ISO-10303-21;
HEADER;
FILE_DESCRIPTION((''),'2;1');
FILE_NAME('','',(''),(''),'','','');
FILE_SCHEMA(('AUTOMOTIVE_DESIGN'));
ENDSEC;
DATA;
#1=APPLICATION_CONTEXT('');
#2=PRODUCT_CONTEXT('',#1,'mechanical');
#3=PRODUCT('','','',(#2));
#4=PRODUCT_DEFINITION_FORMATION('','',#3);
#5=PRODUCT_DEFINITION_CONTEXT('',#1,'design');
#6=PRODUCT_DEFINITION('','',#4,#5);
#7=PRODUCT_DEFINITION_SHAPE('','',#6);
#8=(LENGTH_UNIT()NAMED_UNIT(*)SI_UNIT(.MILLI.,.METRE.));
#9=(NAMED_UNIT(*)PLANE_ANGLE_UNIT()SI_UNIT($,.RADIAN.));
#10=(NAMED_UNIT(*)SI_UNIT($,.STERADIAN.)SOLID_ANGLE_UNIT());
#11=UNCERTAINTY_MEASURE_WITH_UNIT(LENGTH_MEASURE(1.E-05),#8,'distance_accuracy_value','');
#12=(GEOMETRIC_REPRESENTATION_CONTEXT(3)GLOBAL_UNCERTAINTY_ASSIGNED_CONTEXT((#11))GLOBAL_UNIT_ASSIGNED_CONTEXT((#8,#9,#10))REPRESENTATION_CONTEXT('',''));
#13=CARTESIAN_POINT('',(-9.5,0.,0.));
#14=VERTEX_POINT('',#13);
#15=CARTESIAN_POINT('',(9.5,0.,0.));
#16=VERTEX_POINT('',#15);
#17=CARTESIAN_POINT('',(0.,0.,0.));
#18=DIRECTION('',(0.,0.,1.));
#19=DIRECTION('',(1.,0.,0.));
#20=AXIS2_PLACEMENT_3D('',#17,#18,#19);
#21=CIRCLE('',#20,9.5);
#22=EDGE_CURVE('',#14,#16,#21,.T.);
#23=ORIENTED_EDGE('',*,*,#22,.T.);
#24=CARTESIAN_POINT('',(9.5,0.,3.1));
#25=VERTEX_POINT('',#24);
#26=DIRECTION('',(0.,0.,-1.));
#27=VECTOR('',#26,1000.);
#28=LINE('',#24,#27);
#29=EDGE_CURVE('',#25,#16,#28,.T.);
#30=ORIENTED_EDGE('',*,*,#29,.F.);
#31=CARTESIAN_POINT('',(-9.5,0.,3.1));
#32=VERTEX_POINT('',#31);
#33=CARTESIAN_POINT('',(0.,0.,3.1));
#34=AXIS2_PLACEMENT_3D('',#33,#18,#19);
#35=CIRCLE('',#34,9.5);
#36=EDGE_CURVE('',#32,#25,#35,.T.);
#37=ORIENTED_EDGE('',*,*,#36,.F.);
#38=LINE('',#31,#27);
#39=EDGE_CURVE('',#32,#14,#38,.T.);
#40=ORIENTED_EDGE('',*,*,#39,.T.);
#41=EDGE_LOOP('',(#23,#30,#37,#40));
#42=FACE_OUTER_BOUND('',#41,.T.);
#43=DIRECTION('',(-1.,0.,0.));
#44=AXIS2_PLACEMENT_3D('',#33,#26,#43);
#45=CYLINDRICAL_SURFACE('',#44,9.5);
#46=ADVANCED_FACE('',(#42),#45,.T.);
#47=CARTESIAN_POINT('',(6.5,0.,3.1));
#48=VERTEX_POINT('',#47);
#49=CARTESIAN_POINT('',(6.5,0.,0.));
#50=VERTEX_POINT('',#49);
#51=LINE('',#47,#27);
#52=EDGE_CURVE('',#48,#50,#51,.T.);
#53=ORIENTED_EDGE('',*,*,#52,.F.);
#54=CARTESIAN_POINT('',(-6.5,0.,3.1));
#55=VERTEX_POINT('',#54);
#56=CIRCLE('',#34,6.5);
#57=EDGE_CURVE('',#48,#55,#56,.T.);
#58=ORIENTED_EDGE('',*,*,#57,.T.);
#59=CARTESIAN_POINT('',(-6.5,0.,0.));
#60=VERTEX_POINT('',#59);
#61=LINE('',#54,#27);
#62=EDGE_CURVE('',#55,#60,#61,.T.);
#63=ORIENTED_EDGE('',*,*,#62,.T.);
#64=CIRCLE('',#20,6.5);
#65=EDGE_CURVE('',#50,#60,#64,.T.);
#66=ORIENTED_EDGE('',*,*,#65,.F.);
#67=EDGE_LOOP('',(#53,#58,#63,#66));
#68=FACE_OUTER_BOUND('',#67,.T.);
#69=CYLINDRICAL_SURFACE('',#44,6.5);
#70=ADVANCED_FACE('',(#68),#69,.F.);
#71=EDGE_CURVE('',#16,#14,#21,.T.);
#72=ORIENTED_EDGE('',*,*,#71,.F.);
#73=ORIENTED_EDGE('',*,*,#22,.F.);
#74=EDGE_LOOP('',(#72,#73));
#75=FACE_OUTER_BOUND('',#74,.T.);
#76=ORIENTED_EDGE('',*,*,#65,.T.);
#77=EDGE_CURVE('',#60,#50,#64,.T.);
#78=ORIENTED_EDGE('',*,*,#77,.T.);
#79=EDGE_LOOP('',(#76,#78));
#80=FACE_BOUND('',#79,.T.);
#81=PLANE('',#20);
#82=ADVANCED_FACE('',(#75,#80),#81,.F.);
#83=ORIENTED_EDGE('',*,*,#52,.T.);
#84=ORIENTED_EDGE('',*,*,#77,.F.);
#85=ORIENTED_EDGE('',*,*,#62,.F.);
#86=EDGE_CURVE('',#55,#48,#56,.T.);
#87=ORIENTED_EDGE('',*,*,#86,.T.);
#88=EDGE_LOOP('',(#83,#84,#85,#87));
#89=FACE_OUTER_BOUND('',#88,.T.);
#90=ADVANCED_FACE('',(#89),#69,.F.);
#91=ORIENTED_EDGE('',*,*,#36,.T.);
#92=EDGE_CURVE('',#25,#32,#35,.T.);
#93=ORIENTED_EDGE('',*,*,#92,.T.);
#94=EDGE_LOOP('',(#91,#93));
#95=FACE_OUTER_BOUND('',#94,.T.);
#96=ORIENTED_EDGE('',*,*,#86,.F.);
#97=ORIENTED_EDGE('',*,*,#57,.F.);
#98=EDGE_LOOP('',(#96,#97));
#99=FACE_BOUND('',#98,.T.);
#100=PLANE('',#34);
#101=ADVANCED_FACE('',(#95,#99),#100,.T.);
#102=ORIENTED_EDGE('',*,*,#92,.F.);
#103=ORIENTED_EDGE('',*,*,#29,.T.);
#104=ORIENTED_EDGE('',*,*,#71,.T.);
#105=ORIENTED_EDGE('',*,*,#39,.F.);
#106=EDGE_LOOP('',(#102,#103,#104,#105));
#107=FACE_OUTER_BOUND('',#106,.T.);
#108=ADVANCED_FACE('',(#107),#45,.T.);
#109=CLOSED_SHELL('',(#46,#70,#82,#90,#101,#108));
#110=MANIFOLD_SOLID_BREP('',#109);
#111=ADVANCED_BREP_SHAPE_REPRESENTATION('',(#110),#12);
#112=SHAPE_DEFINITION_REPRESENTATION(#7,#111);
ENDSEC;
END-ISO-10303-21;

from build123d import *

# Parameters (mm, degrees)
SKETCH1_R           = 9.5
SKETCH1_R_2         = 6.5
BOSS_EXTRUDE1_DEPTH = 3.1


with BuildPart() as part:
    # Sketch1 → Boss-Extrude1 (new body)
    with BuildSketch(Plane.XY):
        with Locations(Location((0, 0, 0), (0, 0, 180))):
            Circle(SKETCH1_R)
        with Locations(Location((0, 0, 0), (0, 0, 180))):
            Circle(SKETCH1_R_2, mode=Mode.SUBTRACT)
    extrude(amount=BOSS_EXTRUDE1_DEPTH)


solid = part.part
